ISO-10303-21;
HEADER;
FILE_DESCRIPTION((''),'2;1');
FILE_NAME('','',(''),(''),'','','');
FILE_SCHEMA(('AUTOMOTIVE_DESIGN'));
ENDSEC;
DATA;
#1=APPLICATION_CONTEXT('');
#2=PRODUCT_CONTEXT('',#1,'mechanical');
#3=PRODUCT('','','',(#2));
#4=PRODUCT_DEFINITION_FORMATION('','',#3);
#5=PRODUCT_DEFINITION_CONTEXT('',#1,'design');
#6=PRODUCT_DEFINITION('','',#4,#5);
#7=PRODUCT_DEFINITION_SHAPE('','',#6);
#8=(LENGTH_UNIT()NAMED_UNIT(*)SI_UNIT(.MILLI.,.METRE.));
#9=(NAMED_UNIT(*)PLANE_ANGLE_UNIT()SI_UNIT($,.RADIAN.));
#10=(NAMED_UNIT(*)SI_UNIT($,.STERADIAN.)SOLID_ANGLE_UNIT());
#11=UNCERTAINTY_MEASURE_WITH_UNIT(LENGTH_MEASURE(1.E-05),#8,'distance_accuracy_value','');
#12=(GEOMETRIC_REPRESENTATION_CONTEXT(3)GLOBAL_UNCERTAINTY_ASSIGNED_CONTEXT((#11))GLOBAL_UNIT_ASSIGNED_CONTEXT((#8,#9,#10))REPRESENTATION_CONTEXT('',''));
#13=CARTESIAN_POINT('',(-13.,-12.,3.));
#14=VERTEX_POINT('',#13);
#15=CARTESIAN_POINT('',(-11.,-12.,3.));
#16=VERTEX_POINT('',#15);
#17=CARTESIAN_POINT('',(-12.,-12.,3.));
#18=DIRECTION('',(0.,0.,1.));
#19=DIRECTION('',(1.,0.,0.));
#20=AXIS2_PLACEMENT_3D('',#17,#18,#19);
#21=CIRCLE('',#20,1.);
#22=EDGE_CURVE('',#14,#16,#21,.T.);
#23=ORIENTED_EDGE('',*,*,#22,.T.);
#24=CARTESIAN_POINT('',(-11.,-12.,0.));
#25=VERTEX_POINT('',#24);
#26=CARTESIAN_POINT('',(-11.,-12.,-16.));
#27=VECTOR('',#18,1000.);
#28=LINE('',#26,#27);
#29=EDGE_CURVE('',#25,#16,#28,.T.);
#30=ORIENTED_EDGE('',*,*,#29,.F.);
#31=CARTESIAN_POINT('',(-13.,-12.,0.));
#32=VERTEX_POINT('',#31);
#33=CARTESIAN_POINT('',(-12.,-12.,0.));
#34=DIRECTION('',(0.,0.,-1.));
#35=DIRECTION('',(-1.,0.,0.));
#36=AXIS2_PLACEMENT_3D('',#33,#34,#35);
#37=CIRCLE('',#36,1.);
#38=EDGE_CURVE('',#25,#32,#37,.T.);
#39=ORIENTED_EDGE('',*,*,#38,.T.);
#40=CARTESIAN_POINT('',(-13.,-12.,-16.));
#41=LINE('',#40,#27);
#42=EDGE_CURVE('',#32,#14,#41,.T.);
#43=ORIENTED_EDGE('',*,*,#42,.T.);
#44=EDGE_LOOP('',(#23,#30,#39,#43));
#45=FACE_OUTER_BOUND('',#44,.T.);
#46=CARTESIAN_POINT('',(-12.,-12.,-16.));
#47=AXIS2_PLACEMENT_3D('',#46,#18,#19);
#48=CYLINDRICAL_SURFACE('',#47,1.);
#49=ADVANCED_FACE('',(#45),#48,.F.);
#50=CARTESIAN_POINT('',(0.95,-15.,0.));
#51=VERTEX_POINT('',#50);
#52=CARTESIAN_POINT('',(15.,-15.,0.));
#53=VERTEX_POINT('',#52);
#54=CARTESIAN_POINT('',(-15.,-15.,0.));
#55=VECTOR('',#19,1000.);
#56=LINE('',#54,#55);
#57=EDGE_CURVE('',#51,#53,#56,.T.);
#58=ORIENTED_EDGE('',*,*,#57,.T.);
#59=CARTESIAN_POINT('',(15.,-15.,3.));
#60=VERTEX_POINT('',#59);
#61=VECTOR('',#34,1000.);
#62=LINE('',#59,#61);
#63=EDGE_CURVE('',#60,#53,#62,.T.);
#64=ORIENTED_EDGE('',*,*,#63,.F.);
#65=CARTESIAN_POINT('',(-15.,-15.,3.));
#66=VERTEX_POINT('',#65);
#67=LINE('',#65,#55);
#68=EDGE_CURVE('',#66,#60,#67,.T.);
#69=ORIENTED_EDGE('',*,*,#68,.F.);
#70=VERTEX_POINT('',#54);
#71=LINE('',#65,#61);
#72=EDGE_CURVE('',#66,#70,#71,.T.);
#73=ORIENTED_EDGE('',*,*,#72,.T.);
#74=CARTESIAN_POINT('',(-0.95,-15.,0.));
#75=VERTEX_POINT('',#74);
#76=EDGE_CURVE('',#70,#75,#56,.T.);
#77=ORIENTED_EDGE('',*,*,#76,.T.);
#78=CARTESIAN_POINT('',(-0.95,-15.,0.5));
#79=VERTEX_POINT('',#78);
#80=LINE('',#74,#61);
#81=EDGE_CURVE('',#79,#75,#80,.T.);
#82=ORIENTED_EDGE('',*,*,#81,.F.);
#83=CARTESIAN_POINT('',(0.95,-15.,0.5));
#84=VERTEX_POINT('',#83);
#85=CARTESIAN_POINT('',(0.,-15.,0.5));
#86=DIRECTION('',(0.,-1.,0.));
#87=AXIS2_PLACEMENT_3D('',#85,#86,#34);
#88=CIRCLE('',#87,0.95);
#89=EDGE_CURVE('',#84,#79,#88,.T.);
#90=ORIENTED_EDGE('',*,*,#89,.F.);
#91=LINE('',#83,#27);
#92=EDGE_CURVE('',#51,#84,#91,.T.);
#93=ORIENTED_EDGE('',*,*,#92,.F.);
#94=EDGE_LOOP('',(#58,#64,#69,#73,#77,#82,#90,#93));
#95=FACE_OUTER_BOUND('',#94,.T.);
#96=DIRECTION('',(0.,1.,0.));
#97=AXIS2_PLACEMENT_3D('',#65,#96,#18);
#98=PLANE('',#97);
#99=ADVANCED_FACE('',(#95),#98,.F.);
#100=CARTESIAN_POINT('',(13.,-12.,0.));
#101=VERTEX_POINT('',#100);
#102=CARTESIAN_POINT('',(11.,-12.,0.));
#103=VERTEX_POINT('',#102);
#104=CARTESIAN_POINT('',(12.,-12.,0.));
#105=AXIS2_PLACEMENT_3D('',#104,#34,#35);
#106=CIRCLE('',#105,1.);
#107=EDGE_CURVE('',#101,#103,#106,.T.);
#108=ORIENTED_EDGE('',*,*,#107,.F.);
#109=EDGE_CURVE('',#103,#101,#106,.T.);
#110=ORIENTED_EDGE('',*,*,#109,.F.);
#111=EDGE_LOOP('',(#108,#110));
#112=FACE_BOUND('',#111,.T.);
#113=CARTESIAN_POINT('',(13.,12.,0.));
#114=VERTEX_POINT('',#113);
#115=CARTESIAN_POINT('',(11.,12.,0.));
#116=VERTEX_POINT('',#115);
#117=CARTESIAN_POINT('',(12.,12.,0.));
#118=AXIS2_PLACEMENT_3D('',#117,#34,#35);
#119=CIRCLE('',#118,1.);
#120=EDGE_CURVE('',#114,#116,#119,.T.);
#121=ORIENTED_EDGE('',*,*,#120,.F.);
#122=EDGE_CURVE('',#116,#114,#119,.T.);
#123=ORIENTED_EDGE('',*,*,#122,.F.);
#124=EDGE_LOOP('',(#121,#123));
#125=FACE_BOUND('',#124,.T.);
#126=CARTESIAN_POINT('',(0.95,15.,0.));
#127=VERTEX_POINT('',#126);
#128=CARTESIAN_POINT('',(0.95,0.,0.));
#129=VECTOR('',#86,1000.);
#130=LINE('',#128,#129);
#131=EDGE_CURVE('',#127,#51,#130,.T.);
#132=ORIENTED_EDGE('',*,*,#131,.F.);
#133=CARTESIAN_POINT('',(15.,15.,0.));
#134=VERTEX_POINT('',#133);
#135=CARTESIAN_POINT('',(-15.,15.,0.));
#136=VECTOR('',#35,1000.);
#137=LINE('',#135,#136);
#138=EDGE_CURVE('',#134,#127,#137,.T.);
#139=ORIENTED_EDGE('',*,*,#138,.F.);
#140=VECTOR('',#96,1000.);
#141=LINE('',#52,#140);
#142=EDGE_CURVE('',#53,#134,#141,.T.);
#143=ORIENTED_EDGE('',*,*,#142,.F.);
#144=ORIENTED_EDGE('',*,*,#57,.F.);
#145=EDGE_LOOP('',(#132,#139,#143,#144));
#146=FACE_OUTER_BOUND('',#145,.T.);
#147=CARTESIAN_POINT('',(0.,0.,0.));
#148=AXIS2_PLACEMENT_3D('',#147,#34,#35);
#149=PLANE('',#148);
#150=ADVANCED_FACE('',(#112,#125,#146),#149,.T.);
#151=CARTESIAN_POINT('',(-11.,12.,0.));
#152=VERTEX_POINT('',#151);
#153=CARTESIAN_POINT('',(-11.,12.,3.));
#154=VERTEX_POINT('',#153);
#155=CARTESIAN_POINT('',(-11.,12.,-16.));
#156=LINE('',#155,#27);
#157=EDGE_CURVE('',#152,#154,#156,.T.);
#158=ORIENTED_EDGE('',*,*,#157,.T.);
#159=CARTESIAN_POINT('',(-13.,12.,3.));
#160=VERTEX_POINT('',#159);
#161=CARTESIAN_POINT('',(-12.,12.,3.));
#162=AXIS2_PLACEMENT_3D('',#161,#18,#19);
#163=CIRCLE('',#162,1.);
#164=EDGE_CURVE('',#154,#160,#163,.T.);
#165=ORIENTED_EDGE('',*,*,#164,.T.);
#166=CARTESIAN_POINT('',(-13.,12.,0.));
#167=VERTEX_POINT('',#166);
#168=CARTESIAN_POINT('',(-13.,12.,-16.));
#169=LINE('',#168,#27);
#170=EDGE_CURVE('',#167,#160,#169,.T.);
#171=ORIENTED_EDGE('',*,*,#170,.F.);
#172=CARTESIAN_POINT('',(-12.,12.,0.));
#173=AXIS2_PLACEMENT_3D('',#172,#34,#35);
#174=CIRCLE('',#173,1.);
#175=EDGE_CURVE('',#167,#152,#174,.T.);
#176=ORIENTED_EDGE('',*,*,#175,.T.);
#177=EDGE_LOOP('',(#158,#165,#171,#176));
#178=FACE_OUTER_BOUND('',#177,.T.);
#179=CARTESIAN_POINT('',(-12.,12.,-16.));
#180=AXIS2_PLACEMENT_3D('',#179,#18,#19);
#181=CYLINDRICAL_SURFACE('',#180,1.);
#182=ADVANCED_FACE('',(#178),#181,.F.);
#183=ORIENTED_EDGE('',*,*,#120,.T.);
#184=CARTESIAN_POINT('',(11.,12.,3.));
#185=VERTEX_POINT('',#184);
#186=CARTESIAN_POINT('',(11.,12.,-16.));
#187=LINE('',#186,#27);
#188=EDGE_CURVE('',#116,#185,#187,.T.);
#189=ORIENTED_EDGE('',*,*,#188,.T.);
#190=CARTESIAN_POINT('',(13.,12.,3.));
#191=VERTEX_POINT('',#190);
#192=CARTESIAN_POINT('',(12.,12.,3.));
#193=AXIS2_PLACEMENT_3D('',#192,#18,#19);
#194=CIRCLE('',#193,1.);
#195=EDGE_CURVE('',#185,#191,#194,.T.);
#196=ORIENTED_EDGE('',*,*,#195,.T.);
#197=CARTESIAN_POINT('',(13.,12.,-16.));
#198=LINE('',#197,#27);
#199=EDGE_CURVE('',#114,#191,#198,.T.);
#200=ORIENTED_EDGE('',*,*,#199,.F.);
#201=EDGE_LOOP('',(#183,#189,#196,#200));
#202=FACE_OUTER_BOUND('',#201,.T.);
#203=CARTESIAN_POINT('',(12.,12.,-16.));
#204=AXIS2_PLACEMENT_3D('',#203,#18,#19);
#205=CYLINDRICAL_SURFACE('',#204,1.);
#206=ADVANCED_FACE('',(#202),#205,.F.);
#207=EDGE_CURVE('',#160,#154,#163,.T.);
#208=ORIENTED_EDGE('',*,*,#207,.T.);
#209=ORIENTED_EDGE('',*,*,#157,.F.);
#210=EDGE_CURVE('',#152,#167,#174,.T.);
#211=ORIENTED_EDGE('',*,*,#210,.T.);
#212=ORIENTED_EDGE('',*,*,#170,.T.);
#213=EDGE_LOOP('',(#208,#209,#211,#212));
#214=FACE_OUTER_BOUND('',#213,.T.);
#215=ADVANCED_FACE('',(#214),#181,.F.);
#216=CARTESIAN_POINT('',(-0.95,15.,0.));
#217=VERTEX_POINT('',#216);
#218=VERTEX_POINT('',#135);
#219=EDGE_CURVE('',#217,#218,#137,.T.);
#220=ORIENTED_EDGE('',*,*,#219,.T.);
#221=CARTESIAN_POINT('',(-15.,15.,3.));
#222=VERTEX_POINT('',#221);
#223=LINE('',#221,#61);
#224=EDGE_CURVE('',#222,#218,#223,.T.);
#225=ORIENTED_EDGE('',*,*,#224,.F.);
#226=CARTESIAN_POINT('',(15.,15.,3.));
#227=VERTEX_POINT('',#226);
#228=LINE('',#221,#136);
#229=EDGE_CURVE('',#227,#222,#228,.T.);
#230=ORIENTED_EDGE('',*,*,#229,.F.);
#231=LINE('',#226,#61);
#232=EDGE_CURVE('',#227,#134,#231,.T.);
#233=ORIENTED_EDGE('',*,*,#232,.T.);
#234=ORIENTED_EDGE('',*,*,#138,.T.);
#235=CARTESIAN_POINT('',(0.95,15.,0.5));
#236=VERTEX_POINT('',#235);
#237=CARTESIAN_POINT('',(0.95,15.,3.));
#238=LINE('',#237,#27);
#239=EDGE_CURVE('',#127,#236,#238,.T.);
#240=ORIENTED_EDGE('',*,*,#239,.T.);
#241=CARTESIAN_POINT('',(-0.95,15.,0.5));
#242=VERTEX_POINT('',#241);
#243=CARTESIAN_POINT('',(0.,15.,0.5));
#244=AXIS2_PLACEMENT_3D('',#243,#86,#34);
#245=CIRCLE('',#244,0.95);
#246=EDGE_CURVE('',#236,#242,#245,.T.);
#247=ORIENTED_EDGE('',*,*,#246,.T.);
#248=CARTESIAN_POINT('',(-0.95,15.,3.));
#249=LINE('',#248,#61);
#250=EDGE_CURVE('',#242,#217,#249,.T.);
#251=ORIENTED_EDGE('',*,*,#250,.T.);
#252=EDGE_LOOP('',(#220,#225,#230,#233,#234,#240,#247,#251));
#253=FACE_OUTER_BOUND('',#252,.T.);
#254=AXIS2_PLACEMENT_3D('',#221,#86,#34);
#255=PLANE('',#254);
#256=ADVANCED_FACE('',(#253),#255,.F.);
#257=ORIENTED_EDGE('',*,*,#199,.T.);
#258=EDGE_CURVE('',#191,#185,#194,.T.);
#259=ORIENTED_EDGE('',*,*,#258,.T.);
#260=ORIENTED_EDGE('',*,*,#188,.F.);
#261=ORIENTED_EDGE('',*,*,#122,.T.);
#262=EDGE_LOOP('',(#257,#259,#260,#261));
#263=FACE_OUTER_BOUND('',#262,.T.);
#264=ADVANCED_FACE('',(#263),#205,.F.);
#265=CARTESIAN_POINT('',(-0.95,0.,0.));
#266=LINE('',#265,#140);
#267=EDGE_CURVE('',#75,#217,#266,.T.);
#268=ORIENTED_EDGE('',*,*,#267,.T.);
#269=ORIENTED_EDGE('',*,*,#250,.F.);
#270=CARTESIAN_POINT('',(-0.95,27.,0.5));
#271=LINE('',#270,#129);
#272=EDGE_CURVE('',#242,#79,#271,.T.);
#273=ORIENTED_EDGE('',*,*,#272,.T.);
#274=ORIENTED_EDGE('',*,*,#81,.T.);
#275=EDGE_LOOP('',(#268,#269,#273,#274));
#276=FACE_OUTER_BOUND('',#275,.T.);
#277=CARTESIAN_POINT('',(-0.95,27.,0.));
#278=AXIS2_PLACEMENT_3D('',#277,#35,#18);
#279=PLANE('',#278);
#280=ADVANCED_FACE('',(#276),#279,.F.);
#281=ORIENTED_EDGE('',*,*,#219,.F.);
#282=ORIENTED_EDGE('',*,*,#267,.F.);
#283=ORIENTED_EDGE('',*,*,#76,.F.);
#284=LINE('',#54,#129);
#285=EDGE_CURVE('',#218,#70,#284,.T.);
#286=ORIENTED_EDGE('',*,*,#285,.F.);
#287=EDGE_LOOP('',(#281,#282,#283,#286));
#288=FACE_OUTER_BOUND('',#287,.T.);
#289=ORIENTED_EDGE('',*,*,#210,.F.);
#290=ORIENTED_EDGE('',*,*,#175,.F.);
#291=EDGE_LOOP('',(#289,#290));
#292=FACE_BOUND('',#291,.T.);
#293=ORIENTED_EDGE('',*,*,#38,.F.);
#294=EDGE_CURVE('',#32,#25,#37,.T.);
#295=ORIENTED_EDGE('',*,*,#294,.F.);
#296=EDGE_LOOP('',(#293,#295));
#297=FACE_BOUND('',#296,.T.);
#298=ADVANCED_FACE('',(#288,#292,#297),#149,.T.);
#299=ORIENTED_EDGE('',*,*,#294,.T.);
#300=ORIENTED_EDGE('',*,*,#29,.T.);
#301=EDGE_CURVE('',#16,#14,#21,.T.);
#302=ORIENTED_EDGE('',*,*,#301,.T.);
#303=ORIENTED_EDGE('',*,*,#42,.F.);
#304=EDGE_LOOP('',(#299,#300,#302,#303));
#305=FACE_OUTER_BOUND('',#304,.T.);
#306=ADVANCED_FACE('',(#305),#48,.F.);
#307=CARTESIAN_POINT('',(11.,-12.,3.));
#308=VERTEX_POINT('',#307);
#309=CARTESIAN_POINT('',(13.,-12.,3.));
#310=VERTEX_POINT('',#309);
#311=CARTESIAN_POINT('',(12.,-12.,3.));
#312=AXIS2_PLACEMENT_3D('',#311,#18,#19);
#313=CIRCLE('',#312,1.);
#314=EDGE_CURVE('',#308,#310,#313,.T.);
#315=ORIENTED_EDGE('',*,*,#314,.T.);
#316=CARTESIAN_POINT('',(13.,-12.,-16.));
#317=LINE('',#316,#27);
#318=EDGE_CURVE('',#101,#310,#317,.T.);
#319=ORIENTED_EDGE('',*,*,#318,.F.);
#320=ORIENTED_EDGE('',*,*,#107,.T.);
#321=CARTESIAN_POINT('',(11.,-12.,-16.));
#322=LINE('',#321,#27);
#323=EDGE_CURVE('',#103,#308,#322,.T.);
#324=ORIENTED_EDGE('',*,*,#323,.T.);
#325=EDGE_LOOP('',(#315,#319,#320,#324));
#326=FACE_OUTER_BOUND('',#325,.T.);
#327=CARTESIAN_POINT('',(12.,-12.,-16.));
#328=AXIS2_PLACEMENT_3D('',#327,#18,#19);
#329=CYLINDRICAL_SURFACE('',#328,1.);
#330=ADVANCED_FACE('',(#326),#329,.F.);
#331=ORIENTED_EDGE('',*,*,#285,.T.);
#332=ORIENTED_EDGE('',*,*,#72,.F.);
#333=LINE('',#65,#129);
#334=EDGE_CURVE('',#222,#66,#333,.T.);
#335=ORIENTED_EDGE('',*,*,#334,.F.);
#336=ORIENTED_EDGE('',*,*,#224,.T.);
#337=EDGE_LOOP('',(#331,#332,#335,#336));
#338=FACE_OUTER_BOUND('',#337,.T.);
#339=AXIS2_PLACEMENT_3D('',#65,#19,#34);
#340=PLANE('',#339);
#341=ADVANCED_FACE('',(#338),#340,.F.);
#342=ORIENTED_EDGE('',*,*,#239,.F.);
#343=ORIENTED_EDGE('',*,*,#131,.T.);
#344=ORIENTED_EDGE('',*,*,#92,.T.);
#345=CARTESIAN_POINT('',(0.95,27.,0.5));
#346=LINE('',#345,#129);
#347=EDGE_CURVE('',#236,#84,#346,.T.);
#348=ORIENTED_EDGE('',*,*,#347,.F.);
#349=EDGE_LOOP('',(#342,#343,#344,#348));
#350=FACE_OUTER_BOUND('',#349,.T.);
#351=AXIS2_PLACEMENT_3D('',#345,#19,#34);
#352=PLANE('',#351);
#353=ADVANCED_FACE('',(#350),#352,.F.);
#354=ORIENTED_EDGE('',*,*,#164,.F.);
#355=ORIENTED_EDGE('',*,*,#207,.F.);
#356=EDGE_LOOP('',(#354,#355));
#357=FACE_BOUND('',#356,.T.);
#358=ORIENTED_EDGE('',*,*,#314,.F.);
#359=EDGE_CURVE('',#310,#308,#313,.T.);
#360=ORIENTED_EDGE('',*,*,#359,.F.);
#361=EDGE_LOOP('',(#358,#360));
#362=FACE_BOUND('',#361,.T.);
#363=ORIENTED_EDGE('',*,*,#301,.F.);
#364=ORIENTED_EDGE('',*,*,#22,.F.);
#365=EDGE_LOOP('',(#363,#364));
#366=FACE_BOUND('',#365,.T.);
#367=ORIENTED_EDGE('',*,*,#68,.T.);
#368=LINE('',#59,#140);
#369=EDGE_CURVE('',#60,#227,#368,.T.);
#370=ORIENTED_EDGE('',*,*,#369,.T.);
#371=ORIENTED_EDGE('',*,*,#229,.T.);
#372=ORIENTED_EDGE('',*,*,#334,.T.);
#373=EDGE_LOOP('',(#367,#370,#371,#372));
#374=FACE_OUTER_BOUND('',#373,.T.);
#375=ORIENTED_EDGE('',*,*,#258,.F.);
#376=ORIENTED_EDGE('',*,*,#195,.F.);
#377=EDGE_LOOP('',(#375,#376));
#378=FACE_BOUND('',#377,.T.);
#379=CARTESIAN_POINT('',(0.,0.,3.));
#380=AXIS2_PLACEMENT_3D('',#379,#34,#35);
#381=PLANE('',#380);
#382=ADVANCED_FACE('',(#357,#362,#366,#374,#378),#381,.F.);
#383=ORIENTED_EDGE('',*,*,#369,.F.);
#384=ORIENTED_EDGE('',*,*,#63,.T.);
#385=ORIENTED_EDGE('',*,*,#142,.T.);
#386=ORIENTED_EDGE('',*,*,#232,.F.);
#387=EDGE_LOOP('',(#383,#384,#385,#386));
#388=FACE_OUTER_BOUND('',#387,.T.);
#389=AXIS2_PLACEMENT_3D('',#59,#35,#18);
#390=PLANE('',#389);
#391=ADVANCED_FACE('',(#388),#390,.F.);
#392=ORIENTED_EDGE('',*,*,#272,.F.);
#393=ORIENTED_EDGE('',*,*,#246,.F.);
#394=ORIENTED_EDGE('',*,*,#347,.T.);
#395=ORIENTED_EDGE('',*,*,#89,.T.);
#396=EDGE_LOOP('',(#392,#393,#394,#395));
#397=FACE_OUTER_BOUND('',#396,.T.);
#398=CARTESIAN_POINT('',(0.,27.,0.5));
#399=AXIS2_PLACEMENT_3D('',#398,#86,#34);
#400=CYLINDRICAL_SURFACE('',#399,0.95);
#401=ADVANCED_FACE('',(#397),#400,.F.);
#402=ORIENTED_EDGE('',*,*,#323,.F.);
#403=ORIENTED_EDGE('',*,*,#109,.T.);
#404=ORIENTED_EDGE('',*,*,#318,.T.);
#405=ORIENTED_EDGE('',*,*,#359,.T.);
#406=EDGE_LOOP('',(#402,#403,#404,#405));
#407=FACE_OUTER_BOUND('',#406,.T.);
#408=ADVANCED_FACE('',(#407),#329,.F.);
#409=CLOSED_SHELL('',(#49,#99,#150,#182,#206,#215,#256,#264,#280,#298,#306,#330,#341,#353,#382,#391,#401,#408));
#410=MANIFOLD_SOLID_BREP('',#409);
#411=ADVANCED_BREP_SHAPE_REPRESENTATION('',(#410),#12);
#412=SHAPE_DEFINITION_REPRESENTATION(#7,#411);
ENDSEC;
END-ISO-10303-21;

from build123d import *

# Parameters (mm, degrees)
SKETCH1_W           = 30
SKETCH1_H           = 30
BOSS_EXTRUDE1_DEPTH = 3
SKETCH2_R           = 1
CUT_EXTRUDE1_DEPTH  = 19
CUT_EXTRUDE2_DEPTH  = 42


with BuildPart() as part:
    # Sketch1 → Boss-Extrude1 (new body)
    with BuildSketch(Plane.XY):
        Rectangle(SKETCH1_W, SKETCH1_H)
    extrude(amount=BOSS_EXTRUDE1_DEPTH)

    # Sketch2 → Cut-Extrude1 (cut)
    with BuildSketch(Plane.XY.offset(3)):
        with Locations((-12, 12)):
            Circle(SKETCH2_R)
        with Locations((12, 12)):
            Circle(SKETCH2_R)
        with Locations((12, -12)):
            Circle(SKETCH2_R)
        with Locations((-12, -12)):
            Circle(SKETCH2_R)
    extrude(amount=-CUT_EXTRUDE1_DEPTH, mode=Mode.SUBTRACT)

    # Sketch3 → Cut-Extrude2 (cut)
    with BuildSketch(Plane.XZ.offset(15)):
        with BuildLine():
            Line((0.95, 0.5), (0.95, 0))
            Line((0.95, 0), (-0.95, 0))
            Line((-0.95, 0), (-0.95, 0.5))
            ThreePointArc((-0.95, 0.5), (0, 1.45), (0.95, 0.5))
        make_face()
    extrude(amount=-CUT_EXTRUDE2_DEPTH, mode=Mode.SUBTRACT)


solid = part.part
